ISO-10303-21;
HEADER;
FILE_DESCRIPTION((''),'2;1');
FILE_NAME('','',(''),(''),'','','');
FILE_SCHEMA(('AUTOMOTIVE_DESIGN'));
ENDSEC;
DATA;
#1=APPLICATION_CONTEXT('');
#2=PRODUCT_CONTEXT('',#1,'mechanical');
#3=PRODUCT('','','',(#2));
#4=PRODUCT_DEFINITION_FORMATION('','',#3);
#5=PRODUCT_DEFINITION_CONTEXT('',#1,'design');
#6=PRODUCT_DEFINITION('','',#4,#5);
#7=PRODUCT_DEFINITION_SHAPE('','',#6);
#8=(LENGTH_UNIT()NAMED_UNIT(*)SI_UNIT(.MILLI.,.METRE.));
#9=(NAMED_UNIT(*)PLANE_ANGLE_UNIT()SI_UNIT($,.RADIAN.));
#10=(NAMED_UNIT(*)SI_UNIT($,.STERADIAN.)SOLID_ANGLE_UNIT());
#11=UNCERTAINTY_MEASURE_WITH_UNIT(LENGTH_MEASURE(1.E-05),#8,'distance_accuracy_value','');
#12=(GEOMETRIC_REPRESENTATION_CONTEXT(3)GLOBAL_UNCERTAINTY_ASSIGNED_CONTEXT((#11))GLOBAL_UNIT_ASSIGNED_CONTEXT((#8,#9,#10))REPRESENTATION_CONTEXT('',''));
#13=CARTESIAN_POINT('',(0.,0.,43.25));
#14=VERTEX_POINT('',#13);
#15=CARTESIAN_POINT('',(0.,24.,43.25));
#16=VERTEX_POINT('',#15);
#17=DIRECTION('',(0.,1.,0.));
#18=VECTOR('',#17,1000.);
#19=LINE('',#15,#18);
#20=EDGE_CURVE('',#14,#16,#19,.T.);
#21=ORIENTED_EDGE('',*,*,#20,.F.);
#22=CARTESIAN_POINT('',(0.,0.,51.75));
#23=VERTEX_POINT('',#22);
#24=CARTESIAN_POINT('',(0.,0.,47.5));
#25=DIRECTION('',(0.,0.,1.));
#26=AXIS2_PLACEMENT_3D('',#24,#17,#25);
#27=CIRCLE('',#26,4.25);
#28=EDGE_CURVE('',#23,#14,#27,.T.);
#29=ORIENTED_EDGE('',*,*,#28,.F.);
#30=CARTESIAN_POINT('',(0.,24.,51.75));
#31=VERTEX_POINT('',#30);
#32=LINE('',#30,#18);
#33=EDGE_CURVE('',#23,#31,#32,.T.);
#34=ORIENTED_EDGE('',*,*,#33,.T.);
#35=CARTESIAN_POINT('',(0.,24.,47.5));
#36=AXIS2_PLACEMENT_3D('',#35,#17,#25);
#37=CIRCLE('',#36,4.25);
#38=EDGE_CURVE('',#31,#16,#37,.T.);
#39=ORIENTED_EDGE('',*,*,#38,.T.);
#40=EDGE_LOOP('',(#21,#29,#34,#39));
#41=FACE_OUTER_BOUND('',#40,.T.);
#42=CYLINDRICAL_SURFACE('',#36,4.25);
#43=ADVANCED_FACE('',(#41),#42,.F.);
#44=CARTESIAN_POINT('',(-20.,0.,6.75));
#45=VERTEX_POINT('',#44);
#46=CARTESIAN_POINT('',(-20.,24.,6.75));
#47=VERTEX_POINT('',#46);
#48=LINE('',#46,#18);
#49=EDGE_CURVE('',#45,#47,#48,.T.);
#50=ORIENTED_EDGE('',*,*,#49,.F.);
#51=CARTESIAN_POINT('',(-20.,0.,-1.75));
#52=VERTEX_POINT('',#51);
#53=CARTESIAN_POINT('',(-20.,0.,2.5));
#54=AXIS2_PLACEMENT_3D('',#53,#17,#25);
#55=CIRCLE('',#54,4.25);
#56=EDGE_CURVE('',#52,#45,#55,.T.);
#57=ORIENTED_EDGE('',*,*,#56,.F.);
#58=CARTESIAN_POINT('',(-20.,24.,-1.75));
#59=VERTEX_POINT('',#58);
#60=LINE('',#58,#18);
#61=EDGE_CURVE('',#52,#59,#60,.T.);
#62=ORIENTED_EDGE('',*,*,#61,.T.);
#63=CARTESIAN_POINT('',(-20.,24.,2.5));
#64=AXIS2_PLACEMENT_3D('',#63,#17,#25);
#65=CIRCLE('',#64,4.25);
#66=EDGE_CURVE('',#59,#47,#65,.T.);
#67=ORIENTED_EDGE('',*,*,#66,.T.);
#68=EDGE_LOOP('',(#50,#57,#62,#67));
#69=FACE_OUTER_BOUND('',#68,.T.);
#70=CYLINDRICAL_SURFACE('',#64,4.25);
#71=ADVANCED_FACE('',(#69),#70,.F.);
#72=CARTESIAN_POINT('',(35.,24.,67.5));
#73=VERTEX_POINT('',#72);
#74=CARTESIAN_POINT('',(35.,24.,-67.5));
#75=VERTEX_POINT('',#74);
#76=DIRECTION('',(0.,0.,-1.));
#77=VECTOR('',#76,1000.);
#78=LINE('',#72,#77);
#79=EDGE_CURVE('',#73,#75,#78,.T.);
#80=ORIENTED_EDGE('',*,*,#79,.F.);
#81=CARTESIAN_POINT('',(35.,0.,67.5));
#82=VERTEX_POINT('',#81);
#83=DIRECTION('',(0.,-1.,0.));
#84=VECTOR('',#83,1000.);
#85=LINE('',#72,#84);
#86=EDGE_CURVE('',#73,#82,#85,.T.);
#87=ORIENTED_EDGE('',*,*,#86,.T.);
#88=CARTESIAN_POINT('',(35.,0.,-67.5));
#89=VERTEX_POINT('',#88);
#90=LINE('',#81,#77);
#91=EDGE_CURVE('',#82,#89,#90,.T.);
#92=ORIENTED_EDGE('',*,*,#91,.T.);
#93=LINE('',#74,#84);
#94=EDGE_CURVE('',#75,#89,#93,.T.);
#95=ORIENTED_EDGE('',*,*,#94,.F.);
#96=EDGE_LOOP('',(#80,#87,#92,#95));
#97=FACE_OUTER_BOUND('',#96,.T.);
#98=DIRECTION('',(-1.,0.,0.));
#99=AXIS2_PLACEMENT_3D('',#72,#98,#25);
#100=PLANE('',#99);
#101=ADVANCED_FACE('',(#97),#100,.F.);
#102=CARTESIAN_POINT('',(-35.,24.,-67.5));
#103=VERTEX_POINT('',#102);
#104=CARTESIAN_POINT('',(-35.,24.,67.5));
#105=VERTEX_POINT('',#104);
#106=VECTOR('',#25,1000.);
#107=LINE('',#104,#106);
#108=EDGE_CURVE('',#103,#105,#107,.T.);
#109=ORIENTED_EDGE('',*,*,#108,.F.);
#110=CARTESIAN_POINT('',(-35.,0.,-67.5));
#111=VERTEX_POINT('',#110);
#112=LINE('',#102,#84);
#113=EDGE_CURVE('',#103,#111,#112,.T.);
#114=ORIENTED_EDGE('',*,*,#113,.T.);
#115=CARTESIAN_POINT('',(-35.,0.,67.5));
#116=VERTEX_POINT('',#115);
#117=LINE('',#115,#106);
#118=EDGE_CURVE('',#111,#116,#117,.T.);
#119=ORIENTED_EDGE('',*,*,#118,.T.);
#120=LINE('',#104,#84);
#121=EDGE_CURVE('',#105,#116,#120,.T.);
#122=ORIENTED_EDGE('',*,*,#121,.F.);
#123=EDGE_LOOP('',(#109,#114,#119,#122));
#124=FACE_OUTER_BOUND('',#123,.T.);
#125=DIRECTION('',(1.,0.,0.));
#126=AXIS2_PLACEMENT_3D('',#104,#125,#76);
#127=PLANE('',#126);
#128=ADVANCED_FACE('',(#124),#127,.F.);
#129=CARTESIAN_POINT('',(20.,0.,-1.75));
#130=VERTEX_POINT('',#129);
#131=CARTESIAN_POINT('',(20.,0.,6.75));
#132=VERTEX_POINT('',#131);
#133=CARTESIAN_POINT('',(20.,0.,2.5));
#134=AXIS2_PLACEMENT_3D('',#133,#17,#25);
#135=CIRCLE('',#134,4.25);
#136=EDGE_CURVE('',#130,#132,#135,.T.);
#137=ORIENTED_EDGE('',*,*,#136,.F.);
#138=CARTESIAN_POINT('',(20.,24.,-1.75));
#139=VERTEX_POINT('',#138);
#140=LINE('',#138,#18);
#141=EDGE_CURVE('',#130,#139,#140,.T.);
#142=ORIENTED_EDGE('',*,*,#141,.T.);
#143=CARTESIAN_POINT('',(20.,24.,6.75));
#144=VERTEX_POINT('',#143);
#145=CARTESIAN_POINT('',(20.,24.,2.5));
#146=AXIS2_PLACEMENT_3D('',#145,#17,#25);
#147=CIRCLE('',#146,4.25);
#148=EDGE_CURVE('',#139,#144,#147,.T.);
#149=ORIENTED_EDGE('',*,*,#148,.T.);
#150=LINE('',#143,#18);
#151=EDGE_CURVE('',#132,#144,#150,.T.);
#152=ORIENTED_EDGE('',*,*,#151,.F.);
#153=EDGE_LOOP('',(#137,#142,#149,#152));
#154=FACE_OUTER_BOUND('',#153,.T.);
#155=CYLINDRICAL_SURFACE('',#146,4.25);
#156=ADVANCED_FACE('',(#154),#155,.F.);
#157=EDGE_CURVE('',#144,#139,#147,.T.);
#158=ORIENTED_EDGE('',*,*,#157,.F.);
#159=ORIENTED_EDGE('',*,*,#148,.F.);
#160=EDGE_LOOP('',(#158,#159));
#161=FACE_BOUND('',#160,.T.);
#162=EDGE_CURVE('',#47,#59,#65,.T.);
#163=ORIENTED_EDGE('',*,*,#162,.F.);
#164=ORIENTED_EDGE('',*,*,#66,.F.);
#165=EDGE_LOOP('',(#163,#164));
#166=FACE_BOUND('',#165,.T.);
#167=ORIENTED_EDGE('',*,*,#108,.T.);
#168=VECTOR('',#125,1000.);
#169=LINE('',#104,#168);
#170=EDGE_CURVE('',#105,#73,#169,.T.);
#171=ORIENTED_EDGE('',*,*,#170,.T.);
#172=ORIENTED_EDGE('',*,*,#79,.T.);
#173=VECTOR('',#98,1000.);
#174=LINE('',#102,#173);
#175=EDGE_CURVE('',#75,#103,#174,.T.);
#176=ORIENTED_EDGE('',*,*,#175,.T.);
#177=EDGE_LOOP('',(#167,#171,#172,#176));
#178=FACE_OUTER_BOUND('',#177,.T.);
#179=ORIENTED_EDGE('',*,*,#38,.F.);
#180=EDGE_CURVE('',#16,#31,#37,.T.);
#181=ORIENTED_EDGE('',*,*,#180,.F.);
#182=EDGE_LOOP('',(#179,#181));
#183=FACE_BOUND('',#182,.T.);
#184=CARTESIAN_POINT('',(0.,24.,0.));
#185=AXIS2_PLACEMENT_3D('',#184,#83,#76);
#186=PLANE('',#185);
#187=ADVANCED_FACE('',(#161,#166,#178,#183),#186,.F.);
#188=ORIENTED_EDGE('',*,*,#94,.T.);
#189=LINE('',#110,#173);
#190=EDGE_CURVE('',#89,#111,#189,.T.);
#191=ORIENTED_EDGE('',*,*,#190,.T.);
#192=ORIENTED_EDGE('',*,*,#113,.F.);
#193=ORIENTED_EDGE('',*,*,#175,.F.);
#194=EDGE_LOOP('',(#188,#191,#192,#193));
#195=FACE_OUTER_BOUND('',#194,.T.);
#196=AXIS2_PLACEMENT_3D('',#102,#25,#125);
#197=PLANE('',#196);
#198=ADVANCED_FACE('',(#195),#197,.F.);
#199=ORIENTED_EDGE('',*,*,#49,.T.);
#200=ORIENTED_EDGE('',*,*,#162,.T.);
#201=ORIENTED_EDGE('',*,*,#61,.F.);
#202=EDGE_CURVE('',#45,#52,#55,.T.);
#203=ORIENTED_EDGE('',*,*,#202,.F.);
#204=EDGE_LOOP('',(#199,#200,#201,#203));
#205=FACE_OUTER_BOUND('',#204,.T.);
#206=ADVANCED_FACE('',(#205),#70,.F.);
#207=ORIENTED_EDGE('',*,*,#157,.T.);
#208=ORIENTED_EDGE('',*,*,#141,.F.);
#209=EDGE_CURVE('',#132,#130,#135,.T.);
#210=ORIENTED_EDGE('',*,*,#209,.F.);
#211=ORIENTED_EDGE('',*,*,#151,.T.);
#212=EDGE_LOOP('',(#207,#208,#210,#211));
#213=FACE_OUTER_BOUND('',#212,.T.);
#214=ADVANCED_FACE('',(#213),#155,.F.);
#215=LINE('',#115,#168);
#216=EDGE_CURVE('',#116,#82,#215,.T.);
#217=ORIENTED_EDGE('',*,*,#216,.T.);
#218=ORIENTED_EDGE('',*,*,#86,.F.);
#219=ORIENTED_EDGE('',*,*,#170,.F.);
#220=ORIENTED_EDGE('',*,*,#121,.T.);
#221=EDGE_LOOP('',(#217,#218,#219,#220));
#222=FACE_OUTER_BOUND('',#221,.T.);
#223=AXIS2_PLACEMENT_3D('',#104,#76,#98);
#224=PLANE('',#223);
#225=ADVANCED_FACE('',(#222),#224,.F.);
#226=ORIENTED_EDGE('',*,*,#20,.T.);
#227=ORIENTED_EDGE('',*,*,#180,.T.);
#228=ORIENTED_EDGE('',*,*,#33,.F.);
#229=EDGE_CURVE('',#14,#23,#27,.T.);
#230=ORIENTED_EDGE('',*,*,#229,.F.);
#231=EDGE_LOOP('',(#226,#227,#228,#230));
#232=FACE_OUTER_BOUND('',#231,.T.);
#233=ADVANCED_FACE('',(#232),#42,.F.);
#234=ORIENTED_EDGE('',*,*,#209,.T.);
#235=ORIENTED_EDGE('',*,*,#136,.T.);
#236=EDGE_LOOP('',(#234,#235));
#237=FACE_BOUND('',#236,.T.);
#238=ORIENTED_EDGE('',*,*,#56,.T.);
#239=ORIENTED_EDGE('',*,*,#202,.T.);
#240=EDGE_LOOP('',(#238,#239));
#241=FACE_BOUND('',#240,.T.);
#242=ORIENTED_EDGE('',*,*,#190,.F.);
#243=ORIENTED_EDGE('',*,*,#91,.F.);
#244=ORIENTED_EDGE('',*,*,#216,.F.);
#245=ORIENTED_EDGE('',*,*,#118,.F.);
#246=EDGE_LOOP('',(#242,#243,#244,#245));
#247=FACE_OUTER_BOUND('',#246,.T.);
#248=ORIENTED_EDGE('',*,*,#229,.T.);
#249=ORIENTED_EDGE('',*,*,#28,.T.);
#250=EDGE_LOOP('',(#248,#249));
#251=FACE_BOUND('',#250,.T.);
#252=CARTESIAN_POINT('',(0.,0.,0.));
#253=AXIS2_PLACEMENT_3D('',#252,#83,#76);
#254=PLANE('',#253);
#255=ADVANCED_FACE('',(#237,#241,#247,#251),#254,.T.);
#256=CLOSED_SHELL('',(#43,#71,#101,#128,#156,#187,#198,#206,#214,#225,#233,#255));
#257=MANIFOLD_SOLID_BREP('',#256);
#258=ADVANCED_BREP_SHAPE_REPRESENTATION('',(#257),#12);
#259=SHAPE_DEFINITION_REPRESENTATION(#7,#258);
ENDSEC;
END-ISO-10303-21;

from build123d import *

# Parameters (mm, degrees)
SKETCH_1_W          = 70
SKETCH_1_H          = 135
EXTRUDE_1_DEPTH     = 24
HOLE_WIZARD_M10_1_D = 8.5


with BuildPart() as part:
    # 草图1 → 凸台-拉伸1 (new body)
    with BuildSketch(Plane(origin=(0, 0, 0), x_dir=(1, 0, 0), z_dir=(0, 1, 0))):
        Rectangle(SKETCH_1_W, SKETCH_1_H)
    extrude(amount=EXTRUDE_1_DEPTH)

    # M10 螺纹孔1 (through all)
    with Locations(Plane(origin=(0, 24, 0), x_dir=(1, 0, 0), z_dir=(0, 1, 0))):
        with Locations((-20, -2.5), (20, -2.5), (0, -47.5)):
            Hole(HOLE_WIZARD_M10_1_D / 2)


solid = part.part
